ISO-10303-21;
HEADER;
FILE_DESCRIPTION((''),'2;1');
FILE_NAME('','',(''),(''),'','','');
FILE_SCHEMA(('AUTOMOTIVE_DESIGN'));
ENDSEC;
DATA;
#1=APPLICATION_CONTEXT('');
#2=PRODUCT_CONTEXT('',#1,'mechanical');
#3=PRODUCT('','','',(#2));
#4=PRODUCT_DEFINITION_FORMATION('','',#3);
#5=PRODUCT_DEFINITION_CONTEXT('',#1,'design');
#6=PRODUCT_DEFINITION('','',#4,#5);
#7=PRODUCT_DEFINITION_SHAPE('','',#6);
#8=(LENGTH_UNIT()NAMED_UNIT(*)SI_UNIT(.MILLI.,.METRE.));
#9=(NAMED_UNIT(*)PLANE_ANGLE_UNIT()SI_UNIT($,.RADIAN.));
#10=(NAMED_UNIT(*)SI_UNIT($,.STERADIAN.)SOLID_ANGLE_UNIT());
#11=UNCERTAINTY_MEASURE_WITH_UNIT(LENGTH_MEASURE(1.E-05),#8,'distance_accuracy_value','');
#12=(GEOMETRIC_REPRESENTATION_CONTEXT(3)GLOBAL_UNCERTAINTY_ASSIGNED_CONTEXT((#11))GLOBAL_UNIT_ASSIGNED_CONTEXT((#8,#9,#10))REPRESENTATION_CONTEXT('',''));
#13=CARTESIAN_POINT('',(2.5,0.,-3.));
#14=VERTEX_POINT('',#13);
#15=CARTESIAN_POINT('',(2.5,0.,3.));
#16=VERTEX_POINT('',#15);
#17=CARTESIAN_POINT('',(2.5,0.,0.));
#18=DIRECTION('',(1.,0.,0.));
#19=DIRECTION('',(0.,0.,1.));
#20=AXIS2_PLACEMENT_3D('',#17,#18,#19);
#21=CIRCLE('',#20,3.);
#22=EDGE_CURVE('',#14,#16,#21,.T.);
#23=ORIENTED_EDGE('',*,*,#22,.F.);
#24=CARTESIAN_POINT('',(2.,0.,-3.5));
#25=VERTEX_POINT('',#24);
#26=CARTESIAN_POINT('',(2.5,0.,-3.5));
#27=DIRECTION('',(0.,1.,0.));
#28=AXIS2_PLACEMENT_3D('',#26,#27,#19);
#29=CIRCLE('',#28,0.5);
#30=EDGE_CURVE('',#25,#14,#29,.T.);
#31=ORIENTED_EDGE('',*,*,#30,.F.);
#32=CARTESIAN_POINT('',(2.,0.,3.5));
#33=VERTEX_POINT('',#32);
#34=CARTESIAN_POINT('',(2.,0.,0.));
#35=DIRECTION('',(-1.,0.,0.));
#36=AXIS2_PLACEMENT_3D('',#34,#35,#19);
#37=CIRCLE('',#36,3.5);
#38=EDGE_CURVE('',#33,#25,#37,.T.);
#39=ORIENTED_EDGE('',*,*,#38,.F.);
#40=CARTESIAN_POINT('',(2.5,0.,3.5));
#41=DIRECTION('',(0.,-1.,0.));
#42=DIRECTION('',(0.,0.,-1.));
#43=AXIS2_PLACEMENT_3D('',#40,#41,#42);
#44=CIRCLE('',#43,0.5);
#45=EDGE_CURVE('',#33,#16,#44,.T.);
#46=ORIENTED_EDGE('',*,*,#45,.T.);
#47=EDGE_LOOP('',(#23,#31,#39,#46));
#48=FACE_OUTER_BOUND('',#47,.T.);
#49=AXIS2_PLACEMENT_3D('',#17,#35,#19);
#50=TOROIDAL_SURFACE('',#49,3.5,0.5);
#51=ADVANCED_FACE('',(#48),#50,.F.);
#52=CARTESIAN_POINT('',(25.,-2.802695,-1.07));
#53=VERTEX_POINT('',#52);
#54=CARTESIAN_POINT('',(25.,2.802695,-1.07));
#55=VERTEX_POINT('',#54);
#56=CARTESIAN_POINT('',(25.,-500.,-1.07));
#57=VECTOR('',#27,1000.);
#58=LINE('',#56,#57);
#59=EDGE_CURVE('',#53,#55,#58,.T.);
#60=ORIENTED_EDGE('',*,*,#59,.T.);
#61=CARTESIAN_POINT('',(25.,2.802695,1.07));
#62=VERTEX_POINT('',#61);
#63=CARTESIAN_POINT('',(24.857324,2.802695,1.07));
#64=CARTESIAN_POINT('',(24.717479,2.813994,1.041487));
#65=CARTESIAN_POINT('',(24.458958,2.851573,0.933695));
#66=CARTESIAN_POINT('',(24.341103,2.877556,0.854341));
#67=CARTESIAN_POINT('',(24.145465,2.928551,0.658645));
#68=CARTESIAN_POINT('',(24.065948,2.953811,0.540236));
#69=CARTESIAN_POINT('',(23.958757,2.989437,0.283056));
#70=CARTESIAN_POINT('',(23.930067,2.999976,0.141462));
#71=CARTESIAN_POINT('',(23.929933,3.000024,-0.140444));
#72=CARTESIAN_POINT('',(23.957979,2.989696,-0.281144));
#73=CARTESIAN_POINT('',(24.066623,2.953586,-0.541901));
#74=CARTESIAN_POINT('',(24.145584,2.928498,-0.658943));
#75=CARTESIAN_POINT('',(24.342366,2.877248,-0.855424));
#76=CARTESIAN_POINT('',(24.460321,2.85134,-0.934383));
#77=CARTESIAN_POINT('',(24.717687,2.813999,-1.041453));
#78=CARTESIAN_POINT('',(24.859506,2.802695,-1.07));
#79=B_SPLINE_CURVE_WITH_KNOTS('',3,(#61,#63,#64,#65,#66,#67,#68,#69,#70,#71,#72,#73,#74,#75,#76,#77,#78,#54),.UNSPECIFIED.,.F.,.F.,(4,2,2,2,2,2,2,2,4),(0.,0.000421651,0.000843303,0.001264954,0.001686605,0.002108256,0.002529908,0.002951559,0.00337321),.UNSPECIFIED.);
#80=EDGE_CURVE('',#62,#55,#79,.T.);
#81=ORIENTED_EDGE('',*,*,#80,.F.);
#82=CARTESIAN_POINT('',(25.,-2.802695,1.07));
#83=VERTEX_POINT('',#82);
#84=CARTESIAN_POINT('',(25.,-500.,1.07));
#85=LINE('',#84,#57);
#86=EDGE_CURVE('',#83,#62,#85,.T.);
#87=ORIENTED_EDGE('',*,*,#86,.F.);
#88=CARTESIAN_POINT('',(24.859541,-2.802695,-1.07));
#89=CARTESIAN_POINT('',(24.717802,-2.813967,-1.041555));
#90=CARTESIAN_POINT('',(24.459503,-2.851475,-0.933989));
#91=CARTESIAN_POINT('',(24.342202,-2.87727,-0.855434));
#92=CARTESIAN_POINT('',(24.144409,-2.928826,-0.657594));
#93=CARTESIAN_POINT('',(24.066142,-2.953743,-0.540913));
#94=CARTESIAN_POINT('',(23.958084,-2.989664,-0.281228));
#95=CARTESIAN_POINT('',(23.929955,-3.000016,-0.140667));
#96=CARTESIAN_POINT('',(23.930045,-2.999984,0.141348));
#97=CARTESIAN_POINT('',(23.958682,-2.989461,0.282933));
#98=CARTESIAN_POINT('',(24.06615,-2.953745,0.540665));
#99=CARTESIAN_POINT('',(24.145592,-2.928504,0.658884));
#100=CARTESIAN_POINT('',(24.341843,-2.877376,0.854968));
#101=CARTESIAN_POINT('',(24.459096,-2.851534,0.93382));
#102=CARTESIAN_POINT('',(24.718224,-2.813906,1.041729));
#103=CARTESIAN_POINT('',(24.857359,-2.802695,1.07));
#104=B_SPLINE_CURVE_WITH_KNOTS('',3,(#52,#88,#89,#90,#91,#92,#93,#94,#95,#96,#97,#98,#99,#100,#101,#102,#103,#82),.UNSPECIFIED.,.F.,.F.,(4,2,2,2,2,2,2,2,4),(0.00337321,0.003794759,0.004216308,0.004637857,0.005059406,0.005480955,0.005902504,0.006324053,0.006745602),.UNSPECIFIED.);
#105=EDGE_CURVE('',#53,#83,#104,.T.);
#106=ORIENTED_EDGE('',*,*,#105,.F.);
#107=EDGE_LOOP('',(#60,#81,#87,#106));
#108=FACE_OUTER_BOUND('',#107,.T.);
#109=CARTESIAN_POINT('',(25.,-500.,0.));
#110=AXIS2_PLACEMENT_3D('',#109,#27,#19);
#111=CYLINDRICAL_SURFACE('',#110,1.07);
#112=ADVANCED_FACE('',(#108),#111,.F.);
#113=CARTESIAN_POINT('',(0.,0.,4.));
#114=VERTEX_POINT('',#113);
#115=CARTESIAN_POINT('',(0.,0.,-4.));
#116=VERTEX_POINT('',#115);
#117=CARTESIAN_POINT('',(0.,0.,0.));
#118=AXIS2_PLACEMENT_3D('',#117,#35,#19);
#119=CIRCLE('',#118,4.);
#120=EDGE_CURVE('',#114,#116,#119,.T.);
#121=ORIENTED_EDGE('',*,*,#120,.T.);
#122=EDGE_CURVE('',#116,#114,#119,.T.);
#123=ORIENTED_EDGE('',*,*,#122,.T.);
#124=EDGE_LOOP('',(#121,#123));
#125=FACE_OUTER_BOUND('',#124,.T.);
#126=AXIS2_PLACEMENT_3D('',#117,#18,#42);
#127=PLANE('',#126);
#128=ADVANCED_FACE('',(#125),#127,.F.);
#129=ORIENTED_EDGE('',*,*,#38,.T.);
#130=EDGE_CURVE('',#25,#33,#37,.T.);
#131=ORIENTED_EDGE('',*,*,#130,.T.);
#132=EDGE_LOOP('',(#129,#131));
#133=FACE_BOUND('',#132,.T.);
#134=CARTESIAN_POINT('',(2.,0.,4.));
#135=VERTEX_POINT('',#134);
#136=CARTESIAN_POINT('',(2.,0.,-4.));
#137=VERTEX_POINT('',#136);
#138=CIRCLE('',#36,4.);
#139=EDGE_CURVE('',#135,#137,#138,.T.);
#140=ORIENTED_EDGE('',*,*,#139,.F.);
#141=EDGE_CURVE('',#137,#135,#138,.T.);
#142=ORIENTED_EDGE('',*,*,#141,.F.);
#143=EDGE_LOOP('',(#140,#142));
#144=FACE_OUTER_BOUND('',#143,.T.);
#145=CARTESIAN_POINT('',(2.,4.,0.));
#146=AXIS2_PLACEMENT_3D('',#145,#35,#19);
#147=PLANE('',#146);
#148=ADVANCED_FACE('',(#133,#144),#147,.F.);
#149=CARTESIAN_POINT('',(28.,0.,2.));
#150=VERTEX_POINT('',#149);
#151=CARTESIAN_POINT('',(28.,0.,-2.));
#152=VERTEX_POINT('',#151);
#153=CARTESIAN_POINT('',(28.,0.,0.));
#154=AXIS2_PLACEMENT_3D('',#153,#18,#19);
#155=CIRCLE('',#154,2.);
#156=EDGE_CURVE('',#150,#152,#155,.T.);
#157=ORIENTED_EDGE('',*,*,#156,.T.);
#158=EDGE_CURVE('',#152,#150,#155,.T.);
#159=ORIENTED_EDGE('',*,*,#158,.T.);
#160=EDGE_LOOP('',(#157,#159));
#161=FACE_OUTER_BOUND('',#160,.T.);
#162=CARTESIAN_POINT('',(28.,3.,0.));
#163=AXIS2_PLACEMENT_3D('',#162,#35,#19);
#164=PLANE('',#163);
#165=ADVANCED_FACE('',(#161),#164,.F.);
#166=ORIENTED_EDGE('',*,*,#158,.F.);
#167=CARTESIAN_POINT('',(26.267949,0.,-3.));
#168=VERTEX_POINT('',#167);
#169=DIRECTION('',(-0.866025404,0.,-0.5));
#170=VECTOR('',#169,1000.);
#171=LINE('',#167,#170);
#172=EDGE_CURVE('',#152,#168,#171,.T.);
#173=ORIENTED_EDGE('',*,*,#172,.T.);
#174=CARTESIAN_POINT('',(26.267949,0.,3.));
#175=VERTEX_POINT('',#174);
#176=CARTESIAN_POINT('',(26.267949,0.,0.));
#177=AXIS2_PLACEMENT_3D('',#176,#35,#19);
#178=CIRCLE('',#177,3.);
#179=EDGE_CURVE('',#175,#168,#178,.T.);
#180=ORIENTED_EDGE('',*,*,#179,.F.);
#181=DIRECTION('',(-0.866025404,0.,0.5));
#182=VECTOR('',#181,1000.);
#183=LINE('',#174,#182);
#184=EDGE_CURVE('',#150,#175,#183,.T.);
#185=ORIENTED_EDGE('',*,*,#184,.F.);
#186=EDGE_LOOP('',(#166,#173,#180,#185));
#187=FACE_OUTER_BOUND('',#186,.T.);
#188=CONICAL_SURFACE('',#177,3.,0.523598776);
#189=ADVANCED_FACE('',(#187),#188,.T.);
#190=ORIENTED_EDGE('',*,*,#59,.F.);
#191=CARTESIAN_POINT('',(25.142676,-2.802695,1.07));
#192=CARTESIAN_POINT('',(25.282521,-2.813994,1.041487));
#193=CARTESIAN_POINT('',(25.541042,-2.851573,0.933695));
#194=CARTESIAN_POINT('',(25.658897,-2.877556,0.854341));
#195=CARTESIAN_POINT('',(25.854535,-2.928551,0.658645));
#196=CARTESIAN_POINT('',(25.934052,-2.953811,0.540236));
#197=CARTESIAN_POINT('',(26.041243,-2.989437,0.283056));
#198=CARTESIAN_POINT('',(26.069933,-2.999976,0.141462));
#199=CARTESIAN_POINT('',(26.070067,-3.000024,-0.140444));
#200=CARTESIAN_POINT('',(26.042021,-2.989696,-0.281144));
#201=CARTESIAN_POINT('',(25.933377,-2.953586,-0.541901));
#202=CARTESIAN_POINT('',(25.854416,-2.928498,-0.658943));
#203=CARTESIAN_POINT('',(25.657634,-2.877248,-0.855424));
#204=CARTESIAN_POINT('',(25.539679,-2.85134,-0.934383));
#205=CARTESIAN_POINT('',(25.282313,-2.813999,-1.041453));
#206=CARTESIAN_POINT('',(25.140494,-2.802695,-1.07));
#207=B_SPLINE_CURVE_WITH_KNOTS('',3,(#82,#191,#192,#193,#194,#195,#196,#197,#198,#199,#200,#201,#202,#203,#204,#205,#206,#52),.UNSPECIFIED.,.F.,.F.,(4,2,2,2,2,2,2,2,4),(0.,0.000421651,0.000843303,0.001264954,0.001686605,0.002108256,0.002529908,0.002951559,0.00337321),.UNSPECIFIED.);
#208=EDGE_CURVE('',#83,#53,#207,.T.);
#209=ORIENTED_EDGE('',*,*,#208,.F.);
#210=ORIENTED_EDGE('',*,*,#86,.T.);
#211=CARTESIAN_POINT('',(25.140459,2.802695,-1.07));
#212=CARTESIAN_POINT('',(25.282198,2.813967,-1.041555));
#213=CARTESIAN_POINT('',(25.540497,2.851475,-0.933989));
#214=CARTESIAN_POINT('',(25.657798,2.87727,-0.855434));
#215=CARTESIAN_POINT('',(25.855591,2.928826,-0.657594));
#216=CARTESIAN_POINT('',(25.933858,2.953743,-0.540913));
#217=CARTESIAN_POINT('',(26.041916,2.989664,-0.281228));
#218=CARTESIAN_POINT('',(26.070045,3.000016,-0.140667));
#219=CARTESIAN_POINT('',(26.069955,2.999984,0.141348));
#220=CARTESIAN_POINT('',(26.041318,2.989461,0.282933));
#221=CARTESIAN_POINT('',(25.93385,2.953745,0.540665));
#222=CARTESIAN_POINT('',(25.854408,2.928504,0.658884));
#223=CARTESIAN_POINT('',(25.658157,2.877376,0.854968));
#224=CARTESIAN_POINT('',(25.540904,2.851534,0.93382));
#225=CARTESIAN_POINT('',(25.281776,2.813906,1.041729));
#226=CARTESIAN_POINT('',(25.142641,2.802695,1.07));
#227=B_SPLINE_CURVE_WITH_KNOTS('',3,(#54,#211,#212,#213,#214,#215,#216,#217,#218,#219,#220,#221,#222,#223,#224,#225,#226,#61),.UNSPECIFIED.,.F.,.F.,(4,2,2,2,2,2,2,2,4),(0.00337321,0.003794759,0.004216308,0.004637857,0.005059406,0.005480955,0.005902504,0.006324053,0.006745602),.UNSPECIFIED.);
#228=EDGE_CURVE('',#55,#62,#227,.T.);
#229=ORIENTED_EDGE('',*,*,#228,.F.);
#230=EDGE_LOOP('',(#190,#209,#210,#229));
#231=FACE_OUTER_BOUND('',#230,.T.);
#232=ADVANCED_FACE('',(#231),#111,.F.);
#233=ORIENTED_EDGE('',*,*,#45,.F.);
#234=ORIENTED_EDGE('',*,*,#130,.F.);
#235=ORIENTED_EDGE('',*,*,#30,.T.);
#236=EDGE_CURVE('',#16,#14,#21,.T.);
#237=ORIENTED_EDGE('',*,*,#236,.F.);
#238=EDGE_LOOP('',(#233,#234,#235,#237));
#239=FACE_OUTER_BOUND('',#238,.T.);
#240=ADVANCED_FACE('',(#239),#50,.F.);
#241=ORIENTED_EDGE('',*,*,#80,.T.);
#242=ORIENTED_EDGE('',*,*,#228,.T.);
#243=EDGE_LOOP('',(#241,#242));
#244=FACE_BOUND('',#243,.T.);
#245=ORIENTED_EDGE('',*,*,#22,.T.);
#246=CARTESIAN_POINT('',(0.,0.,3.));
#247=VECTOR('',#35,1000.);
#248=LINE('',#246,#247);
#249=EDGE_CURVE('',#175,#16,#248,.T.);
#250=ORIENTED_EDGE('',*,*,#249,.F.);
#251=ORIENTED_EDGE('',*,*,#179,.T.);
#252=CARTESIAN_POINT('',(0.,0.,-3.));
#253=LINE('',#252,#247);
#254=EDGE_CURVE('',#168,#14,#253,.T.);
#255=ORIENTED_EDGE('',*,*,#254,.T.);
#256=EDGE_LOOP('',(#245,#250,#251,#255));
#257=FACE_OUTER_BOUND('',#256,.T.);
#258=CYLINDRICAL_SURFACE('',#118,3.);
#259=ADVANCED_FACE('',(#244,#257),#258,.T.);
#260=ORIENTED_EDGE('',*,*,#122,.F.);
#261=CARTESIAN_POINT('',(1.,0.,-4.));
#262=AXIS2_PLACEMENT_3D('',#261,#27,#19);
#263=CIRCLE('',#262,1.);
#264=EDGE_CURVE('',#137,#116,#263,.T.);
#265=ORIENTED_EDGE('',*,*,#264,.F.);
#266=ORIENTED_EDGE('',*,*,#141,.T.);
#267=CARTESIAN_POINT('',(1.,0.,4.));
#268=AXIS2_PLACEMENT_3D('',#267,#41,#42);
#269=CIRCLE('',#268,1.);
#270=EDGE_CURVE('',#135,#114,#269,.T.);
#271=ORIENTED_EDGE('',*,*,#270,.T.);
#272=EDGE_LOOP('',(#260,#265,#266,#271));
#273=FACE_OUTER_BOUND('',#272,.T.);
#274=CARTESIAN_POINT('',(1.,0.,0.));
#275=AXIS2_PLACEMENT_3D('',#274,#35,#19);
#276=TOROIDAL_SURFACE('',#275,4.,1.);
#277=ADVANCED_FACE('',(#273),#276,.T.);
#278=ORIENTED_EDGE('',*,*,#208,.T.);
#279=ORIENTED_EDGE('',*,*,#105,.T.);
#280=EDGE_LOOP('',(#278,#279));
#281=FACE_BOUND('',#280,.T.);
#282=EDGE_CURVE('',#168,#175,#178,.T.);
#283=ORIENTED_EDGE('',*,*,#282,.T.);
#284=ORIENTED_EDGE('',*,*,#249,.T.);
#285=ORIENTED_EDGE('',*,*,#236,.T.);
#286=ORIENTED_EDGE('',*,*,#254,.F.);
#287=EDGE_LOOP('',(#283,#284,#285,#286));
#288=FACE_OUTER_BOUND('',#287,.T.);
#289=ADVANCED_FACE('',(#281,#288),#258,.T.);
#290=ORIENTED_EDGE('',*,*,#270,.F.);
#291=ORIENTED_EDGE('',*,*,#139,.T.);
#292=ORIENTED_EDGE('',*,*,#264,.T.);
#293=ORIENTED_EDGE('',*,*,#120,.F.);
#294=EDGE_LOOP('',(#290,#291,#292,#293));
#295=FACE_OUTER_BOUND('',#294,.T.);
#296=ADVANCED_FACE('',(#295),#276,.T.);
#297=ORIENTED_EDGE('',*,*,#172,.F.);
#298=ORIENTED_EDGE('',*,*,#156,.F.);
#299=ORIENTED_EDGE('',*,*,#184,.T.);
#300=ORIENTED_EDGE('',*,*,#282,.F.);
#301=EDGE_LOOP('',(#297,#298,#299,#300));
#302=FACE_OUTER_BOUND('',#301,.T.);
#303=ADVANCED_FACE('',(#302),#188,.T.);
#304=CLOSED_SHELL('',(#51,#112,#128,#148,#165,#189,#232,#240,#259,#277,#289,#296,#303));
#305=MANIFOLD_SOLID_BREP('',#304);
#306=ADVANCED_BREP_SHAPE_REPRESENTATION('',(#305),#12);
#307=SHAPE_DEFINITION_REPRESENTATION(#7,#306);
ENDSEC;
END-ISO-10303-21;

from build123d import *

# Parameters (mm, degrees)
FILLET_1_R          = 0.5
CHAMFER_1_SIZE      = 1.732050808
CHAMFER_1_SIZE2     = 1
SKETCH_2_R          = 1.07
CUT_EXTRUDE_1_DEPTH = 500


with BuildPart() as part:
    # 草图1 → Revolve 730 (revolve)
    with BuildSketch(Plane.XY, mode=Mode.PRIVATE) as revolve_730_sk:
        with BuildLine():
            Line((0, 0), (28, 0))
            Line((28, 0), (28, 3))
            Line((28, 3), (2, 3))
            Line((2, 3), (2, 4))
            ThreePointArc((2, 4), (1, 5), (0, 4))
            Line((0, 4), (0, 0))
        make_face()
    revolve(revolve_730_sk.sketch.rotate(Axis((0, 0, 0), (1, 0, 0)), 90), axis=Axis((0, 0, 0), (1, 0, 0)))

    # 圆角1
    fillet_1_edges = [part.edges().sort_by_distance(p)[0] for p in [
        (2, 0, -3),
    ]]
    fillet(fillet_1_edges, radius=FILLET_1_R)

    # 倒角1
    chamfer_1_edges = [part.edges().sort_by_distance(p)[0] for p in [
        (28, 0, -3),
    ]]
    chamfer_1_side = [part.faces().sort_by_distance(p)[0] for p in [
        (15.25, 0, -3),
    ]]
    chamfer(chamfer_1_edges, length=CHAMFER_1_SIZE, length2=CHAMFER_1_SIZE2, reference=chamfer_1_side[0])

    # 草图2 → 切除-拉伸1 (cut, symmetric)
    with BuildSketch(Plane(origin=(0, 0, 0), x_dir=(1, 0, 0), z_dir=(0, 1, 0))):
        with Locations(Location((25, 0, 0), (0, 0, 270))):
            Circle(SKETCH_2_R)
    extrude(amount=CUT_EXTRUDE_1_DEPTH, both=True, mode=Mode.SUBTRACT)


solid = part.part
